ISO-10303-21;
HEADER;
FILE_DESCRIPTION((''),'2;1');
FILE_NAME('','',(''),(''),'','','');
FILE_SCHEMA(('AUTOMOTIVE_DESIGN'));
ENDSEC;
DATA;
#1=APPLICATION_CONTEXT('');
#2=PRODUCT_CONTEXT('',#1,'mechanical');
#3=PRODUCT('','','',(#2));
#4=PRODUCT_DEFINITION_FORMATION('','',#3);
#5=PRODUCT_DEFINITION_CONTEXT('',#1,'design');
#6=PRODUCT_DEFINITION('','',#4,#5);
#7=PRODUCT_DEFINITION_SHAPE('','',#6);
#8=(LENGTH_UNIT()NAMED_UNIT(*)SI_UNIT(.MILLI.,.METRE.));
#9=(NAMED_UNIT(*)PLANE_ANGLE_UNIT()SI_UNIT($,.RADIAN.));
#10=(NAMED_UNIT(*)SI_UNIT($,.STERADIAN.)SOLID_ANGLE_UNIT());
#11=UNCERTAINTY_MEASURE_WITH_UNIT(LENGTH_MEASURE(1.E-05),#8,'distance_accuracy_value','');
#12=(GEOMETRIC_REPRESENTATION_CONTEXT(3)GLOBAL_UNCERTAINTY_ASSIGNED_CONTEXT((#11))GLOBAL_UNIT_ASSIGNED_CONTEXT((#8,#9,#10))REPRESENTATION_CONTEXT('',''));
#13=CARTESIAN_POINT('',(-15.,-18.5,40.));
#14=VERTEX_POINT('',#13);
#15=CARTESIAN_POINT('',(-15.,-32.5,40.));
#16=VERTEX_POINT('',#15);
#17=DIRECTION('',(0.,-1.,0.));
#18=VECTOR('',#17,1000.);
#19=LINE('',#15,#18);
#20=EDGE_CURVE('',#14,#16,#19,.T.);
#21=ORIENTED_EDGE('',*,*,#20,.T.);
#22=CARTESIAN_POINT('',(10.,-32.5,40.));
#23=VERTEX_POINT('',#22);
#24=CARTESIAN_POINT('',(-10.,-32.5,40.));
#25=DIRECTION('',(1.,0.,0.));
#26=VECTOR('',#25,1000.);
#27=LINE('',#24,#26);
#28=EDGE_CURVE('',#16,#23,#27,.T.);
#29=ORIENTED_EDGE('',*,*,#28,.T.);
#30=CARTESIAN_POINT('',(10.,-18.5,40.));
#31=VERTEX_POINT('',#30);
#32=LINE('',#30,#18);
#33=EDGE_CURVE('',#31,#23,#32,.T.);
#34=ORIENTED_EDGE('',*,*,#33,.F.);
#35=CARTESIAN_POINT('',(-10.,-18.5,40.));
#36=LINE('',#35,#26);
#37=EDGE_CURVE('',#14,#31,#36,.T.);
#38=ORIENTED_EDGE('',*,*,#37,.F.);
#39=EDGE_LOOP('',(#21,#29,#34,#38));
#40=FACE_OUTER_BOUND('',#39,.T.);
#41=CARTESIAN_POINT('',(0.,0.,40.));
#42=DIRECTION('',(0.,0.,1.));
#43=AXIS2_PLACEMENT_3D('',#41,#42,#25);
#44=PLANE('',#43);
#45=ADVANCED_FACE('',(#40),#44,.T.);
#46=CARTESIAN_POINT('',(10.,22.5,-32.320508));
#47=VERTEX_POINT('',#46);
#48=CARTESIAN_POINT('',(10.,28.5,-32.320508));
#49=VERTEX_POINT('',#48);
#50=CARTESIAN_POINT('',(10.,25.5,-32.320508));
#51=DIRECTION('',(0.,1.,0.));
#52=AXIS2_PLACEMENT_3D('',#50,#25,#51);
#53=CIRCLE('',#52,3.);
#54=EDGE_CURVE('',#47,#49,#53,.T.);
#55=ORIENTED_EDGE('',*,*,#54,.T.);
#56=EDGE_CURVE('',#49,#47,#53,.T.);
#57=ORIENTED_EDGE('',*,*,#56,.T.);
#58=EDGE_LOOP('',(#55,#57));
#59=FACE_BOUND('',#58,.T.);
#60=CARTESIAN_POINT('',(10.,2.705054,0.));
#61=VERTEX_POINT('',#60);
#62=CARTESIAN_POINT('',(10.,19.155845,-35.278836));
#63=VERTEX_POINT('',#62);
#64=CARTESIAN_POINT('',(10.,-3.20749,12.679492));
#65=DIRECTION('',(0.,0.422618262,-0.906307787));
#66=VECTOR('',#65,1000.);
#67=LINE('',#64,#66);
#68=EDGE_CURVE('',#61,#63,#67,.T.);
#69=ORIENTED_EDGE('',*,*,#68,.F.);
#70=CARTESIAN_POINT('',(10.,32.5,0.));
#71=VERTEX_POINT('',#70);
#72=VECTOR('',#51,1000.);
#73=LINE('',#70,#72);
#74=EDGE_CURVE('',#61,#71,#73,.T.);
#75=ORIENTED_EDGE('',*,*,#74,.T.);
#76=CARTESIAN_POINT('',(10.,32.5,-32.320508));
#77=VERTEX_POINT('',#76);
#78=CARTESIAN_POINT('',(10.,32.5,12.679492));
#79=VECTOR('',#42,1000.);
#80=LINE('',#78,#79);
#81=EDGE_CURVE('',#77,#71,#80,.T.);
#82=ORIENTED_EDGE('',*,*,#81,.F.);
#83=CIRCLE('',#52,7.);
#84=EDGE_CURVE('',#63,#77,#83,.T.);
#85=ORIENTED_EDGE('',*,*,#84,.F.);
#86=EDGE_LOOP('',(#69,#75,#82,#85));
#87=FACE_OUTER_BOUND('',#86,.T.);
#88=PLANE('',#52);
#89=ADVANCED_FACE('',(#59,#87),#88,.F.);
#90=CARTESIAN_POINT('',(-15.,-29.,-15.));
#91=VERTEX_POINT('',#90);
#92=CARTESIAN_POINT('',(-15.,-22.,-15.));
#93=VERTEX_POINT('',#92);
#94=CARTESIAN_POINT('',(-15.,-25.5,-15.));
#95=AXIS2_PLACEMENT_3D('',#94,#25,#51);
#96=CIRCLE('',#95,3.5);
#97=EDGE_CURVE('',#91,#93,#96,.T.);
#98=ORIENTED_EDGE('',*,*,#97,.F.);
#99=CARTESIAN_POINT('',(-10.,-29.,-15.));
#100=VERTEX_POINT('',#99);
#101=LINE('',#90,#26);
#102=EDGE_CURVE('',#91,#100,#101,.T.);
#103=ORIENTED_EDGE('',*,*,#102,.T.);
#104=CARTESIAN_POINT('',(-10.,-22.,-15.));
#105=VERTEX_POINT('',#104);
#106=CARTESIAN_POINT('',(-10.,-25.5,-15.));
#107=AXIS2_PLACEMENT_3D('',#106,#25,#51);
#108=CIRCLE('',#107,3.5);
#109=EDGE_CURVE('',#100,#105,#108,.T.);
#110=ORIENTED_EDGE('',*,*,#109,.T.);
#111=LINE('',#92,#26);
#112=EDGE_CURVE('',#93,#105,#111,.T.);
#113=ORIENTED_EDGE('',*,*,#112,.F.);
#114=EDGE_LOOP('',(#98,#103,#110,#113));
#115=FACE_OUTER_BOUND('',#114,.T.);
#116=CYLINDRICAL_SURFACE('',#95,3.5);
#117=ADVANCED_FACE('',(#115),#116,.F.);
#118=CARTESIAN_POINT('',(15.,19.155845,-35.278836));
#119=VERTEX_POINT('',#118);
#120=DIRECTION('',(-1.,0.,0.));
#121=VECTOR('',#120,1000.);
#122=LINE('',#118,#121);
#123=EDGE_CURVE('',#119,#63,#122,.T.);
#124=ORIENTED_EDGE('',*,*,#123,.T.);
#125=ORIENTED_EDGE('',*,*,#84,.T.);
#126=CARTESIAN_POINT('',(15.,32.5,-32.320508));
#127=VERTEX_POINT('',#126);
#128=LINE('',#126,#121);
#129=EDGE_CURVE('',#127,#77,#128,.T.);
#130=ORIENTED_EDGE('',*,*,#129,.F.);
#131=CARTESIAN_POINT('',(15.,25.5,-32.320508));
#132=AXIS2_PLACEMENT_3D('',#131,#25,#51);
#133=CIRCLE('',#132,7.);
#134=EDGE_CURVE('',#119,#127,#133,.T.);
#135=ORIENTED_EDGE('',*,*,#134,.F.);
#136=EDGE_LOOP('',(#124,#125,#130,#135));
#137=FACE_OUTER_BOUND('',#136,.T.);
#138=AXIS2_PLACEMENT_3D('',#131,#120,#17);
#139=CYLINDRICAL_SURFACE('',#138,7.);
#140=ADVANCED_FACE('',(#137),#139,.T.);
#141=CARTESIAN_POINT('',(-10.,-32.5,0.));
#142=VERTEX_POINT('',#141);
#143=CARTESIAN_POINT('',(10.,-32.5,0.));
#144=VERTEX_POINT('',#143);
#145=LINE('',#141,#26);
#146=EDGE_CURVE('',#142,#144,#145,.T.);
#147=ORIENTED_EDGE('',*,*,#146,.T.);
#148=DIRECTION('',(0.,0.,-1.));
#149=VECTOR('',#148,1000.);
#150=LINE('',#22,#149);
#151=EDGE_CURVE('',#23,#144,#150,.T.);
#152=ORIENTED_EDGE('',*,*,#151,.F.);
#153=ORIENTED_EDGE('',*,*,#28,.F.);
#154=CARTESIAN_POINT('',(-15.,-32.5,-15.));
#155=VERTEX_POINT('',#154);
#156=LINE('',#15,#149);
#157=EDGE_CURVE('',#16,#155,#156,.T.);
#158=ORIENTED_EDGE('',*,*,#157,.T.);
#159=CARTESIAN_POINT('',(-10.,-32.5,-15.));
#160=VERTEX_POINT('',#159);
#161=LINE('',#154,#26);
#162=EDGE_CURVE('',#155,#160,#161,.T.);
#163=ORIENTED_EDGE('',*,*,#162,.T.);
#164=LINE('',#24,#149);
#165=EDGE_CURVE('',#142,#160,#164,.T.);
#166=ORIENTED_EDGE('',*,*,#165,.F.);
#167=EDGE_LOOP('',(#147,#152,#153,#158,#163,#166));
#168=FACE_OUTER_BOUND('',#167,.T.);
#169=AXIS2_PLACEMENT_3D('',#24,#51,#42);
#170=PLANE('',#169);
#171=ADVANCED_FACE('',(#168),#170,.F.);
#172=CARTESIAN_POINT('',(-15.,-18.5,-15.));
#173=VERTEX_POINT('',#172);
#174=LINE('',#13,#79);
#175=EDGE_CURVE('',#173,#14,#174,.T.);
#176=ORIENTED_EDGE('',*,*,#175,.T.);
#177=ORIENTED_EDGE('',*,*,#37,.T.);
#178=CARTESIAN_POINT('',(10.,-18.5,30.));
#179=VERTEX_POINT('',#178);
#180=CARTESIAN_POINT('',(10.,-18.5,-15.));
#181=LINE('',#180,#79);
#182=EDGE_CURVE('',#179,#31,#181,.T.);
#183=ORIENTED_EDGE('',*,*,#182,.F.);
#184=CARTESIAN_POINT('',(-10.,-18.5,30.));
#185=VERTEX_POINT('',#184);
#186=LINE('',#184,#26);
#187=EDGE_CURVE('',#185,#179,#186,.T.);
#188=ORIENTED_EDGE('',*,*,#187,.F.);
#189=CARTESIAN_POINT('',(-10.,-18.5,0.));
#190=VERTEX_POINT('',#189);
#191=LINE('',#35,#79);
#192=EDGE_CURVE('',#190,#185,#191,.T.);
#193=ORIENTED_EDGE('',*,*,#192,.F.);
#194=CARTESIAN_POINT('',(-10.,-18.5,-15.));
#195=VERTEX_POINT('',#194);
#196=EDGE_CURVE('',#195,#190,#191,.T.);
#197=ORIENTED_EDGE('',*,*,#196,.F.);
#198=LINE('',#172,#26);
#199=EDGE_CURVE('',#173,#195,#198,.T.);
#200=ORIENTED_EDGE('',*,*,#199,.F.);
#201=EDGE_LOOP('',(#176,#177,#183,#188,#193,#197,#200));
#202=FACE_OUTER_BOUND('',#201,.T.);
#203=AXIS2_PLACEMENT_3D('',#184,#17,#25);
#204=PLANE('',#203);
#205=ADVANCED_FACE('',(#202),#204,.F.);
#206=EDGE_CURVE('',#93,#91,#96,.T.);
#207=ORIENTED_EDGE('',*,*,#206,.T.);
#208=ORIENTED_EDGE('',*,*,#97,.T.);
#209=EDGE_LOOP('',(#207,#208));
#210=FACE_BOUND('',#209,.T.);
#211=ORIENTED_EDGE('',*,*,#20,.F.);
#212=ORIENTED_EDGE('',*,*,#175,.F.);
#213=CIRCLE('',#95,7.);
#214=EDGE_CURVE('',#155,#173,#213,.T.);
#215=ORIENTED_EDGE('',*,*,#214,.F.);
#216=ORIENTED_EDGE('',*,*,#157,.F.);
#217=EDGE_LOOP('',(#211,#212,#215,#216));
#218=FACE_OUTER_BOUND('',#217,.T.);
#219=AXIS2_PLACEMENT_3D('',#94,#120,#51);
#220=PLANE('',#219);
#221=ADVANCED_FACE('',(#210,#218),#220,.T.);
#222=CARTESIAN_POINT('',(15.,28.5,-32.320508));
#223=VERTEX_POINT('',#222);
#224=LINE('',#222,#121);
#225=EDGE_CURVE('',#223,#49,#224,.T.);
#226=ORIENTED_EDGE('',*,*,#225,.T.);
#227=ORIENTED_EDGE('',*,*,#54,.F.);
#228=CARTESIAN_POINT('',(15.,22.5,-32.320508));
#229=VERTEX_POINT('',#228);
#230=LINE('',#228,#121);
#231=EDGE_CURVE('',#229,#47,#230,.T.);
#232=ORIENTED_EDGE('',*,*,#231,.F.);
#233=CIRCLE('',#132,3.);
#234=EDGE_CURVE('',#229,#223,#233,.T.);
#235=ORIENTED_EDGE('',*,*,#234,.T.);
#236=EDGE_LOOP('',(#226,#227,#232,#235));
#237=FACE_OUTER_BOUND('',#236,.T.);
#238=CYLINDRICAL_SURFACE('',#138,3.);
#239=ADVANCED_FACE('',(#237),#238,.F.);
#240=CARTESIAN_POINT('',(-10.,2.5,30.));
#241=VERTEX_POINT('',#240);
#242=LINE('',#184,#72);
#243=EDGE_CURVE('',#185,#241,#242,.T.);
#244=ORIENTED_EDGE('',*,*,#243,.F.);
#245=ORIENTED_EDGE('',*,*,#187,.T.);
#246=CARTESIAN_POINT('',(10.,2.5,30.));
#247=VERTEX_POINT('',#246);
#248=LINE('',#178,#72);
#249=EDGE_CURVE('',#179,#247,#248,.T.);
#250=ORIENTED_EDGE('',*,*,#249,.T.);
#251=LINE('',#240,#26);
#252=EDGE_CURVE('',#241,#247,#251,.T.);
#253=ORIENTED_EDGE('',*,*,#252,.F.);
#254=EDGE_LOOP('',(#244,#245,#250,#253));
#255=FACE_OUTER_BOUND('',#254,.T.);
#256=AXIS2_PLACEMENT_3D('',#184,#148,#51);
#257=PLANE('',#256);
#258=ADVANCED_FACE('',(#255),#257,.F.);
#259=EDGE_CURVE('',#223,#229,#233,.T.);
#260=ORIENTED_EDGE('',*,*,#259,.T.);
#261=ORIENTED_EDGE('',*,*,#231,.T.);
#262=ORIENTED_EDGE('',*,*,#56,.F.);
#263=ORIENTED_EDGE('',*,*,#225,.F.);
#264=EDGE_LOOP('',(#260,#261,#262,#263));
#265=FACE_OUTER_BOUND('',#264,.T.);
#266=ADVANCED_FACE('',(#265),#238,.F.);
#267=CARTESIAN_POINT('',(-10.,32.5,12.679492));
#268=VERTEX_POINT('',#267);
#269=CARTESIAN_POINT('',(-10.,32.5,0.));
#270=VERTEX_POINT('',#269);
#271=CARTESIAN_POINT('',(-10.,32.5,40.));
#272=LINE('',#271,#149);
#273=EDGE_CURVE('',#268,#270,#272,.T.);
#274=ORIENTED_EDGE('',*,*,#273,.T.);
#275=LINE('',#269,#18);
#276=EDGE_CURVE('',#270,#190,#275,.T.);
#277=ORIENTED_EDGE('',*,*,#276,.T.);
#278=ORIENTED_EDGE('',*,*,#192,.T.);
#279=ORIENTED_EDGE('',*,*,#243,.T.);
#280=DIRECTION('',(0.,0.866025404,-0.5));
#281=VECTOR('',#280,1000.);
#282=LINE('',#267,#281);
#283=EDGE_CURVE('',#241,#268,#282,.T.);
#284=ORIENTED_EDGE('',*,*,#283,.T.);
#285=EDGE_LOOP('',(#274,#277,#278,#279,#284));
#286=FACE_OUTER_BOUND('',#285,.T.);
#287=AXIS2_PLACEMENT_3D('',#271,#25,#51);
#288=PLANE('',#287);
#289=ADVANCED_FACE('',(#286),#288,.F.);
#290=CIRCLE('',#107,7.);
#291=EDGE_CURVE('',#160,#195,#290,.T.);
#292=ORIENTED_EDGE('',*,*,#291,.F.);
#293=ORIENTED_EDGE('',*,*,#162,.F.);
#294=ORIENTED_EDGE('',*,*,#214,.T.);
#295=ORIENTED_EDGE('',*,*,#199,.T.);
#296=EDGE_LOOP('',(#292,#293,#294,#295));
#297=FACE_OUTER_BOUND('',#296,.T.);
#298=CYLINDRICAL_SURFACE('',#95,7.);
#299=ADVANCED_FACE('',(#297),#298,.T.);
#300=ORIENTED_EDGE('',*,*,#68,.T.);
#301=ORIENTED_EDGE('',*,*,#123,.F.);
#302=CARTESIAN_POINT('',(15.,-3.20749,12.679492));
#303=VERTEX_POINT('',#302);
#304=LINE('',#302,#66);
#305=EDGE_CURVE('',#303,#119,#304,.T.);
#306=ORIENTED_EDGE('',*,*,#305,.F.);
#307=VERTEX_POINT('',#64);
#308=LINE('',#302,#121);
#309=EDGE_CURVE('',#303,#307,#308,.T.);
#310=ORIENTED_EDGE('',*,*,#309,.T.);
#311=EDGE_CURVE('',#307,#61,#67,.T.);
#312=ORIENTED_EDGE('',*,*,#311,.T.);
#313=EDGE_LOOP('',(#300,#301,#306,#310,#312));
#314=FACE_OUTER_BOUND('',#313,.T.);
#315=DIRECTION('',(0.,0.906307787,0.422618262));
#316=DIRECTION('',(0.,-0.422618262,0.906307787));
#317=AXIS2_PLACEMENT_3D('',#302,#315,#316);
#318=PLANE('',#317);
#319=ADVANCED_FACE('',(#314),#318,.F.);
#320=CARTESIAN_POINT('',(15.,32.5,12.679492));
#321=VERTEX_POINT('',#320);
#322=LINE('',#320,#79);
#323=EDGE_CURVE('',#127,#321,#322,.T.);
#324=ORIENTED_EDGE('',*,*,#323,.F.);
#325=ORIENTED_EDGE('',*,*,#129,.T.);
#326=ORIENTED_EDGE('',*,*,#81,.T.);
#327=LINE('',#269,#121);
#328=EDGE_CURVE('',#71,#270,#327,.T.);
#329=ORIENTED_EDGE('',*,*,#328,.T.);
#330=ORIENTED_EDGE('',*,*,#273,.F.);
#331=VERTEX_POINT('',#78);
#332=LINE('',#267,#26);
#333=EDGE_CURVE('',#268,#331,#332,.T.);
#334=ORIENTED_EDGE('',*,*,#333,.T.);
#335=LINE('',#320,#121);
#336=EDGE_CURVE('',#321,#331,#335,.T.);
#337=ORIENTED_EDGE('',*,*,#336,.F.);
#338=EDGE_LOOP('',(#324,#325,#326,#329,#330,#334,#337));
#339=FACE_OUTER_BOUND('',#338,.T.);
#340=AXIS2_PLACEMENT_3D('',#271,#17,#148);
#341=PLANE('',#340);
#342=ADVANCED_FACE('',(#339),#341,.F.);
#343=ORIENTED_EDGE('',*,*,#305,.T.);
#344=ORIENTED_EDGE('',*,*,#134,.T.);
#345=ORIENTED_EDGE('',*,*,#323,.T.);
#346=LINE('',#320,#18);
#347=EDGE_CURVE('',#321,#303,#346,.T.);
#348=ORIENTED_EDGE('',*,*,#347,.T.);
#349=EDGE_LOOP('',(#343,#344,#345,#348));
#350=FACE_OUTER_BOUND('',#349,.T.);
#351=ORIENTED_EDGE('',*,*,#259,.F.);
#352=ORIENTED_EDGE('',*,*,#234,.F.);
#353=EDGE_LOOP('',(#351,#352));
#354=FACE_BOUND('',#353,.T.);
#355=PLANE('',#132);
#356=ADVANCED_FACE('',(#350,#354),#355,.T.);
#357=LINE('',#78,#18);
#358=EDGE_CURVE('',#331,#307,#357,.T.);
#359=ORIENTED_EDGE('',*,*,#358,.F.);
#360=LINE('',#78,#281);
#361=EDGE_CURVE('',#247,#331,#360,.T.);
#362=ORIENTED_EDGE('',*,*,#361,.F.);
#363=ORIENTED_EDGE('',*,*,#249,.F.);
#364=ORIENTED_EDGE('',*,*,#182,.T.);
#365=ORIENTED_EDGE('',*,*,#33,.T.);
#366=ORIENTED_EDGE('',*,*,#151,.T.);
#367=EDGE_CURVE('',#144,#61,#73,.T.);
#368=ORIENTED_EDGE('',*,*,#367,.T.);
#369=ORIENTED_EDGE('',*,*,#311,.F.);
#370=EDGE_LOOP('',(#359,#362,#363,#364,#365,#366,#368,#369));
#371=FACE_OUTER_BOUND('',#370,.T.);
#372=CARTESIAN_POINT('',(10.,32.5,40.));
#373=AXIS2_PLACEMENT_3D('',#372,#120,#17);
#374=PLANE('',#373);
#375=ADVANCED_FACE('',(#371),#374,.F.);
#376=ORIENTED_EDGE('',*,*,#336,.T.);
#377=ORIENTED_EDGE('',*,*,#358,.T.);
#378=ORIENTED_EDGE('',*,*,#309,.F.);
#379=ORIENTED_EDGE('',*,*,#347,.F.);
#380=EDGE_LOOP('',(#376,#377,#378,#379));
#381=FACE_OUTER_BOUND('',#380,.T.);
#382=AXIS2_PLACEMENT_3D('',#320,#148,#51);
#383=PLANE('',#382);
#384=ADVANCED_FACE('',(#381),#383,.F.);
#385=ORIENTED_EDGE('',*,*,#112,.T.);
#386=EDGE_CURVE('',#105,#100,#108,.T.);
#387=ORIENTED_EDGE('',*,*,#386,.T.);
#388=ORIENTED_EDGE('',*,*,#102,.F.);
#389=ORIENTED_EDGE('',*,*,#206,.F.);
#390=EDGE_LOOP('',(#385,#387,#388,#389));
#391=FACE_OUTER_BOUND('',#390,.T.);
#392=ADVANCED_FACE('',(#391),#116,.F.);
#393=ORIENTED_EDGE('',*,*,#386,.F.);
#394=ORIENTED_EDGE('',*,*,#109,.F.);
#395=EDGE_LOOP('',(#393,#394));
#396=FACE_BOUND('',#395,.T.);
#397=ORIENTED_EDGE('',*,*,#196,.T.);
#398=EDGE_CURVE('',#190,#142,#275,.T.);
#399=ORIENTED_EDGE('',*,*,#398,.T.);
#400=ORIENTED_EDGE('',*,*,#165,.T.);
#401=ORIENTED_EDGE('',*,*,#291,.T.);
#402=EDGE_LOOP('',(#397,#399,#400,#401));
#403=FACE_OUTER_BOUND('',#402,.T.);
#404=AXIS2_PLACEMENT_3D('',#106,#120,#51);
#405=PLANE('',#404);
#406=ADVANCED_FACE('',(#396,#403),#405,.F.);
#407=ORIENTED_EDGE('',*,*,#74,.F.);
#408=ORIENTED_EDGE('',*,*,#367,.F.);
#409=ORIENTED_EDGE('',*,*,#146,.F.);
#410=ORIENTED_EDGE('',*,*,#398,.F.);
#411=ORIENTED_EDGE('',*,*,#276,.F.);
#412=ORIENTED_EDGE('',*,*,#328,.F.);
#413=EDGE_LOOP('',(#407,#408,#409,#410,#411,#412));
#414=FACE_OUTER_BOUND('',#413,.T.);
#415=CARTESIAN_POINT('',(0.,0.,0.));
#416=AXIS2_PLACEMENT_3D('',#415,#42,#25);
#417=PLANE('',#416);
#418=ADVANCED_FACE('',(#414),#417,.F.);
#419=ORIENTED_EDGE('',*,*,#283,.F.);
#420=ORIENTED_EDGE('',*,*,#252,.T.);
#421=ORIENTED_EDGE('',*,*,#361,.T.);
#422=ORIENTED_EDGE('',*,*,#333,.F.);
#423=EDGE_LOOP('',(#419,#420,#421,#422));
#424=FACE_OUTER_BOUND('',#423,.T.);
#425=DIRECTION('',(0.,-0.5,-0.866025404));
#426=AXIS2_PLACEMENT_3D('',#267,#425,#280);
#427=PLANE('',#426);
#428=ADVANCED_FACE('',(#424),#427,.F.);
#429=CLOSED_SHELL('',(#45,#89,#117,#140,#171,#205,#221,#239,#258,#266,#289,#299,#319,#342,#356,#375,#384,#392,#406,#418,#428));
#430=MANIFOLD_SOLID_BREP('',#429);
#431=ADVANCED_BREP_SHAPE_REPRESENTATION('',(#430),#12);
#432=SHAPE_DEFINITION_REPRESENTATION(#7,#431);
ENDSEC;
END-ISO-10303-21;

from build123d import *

# Parameters (mm, degrees)
BASE_BLOCK_SKETCH_W         = 20
BASE_BLOCK_SKETCH_H         = 65
BASE_BLOCK_DEPTH            = 40
ANGLED_CUT_30DEG_DEPTH      = 56.283360969
ANGLED_CUT_30DEG_DEPTH_BACK = 56.283360969
SIDE_PAD_DEPTH              = 5
PAD_TRIM_CUT_DEPTH          = 60.634302209
PAD_TRIM_CUT_DEPTH_BACK     = 5
PIN_HOLE_SKETCH_R           = 3.5
PIN_HOLE_7_DEPTH            = 5
LEVER_ARM_SKETCH_R          = 3
LEVER_ARM_DEPTH             = 5


with BuildPart() as part:
    # Base Block Sketch → Base Block (new body)
    with BuildSketch(Plane.XY):
        Rectangle(BASE_BLOCK_SKETCH_W, BASE_BLOCK_SKETCH_H)
    extrude(amount=BASE_BLOCK_DEPTH)

    # Angled Cut Sketch → Angled Cut 30deg (cut, two sides: drawn at the far end of the back side and taken through both)
    with BuildSketch(Plane(origin=(10, 0, 0), x_dir=(0, 0, -1), z_dir=(1, 0, 0)).offset(-ANGLED_CUT_30DEG_DEPTH_BACK)):
        Polygon((-12.679491924, 32.5), (-30, 2.5), (-30, -18.5), (-40, -18.5), (-40, 32.5), align=None)
    extrude(amount=ANGLED_CUT_30DEG_DEPTH + ANGLED_CUT_30DEG_DEPTH_BACK, mode=Mode.SUBTRACT)

    # Side Pad Sketch → Side Pad (add)
    with BuildSketch(Plane(origin=(10, 0, 0), x_dir=(0, 0, -1), z_dir=(1, 0, 0))):
        with BuildLine():
            Line((-40, -32.5), (15, -32.5))
            ThreePointArc((15, -32.5), (22, -25.5), (15, -18.5))
            Line((15, -18.5), (-40, -18.5))
            Line((-40, -18.5), (-40, -32.5))
        make_face()
    side_pad = extrude(amount=SIDE_PAD_DEPTH)

    # Side Pad Mirror: Side Pad across plane
    add(side_pad.mirror(Plane(origin=(0, 0, 0), x_dir=(0, 0, 1), z_dir=(1, 0, 0))))

    # Pad Trim Sketch → Pad Trim Cut (cut, two sides: drawn at the far end of the back side and taken through both)
    with BuildSketch(Plane(origin=(15, 0, 0), x_dir=(0, 0, -1), z_dir=(1, 0, 0)).offset(-PAD_TRIM_CUT_DEPTH_BACK)):
        with BuildLine():
            Line((-40, -18.5), (-40, -32.5))
            Line((-40, -32.5), (15, -32.5))
            ThreePointArc((15, -32.5), (22, -25.5), (15, -18.5))
            Line((15, -18.5), (-40, -18.5))
        make_face()
    extrude(amount=PAD_TRIM_CUT_DEPTH + PAD_TRIM_CUT_DEPTH_BACK, mode=Mode.SUBTRACT)

    # Pin Hole Sketch → Pin Hole Ø7 (cut)
    with BuildSketch(Plane(origin=(-10, 0, 0), x_dir=(0, 0, -1), z_dir=(1, 0, 0))):
        with Locations(Location((15, -25.5, 0), (0, 0, 90))):
            Circle(PIN_HOLE_SKETCH_R)
    extrude(amount=-PIN_HOLE_7_DEPTH, mode=Mode.SUBTRACT)

    # Lever Arm Sketch → Lever Arm (add)
    with BuildSketch(Plane(origin=(10, 0, 0), x_dir=(0, 0, -1), z_dir=(1, 0, 0))):
        with BuildLine():
            Line((-12.679491924, 32.5), (-12.679491924, -3.20749005))
            Line((-12.679491924, -3.20749005), (35.278835908, 19.155845491))
            ThreePointArc((35.278835908, 19.155845491), (39.154580126, 27.015077298), (32.320508076, 32.5))
            Line((32.320508076, 32.5), (-12.679491924, 32.5))
        make_face()
        with Locations(Location((32.320508076, 25.5, 0), (0, 0, 90))):
            Circle(LEVER_ARM_SKETCH_R, mode=Mode.SUBTRACT)
    extrude(amount=LEVER_ARM_DEPTH)


solid = part.part
